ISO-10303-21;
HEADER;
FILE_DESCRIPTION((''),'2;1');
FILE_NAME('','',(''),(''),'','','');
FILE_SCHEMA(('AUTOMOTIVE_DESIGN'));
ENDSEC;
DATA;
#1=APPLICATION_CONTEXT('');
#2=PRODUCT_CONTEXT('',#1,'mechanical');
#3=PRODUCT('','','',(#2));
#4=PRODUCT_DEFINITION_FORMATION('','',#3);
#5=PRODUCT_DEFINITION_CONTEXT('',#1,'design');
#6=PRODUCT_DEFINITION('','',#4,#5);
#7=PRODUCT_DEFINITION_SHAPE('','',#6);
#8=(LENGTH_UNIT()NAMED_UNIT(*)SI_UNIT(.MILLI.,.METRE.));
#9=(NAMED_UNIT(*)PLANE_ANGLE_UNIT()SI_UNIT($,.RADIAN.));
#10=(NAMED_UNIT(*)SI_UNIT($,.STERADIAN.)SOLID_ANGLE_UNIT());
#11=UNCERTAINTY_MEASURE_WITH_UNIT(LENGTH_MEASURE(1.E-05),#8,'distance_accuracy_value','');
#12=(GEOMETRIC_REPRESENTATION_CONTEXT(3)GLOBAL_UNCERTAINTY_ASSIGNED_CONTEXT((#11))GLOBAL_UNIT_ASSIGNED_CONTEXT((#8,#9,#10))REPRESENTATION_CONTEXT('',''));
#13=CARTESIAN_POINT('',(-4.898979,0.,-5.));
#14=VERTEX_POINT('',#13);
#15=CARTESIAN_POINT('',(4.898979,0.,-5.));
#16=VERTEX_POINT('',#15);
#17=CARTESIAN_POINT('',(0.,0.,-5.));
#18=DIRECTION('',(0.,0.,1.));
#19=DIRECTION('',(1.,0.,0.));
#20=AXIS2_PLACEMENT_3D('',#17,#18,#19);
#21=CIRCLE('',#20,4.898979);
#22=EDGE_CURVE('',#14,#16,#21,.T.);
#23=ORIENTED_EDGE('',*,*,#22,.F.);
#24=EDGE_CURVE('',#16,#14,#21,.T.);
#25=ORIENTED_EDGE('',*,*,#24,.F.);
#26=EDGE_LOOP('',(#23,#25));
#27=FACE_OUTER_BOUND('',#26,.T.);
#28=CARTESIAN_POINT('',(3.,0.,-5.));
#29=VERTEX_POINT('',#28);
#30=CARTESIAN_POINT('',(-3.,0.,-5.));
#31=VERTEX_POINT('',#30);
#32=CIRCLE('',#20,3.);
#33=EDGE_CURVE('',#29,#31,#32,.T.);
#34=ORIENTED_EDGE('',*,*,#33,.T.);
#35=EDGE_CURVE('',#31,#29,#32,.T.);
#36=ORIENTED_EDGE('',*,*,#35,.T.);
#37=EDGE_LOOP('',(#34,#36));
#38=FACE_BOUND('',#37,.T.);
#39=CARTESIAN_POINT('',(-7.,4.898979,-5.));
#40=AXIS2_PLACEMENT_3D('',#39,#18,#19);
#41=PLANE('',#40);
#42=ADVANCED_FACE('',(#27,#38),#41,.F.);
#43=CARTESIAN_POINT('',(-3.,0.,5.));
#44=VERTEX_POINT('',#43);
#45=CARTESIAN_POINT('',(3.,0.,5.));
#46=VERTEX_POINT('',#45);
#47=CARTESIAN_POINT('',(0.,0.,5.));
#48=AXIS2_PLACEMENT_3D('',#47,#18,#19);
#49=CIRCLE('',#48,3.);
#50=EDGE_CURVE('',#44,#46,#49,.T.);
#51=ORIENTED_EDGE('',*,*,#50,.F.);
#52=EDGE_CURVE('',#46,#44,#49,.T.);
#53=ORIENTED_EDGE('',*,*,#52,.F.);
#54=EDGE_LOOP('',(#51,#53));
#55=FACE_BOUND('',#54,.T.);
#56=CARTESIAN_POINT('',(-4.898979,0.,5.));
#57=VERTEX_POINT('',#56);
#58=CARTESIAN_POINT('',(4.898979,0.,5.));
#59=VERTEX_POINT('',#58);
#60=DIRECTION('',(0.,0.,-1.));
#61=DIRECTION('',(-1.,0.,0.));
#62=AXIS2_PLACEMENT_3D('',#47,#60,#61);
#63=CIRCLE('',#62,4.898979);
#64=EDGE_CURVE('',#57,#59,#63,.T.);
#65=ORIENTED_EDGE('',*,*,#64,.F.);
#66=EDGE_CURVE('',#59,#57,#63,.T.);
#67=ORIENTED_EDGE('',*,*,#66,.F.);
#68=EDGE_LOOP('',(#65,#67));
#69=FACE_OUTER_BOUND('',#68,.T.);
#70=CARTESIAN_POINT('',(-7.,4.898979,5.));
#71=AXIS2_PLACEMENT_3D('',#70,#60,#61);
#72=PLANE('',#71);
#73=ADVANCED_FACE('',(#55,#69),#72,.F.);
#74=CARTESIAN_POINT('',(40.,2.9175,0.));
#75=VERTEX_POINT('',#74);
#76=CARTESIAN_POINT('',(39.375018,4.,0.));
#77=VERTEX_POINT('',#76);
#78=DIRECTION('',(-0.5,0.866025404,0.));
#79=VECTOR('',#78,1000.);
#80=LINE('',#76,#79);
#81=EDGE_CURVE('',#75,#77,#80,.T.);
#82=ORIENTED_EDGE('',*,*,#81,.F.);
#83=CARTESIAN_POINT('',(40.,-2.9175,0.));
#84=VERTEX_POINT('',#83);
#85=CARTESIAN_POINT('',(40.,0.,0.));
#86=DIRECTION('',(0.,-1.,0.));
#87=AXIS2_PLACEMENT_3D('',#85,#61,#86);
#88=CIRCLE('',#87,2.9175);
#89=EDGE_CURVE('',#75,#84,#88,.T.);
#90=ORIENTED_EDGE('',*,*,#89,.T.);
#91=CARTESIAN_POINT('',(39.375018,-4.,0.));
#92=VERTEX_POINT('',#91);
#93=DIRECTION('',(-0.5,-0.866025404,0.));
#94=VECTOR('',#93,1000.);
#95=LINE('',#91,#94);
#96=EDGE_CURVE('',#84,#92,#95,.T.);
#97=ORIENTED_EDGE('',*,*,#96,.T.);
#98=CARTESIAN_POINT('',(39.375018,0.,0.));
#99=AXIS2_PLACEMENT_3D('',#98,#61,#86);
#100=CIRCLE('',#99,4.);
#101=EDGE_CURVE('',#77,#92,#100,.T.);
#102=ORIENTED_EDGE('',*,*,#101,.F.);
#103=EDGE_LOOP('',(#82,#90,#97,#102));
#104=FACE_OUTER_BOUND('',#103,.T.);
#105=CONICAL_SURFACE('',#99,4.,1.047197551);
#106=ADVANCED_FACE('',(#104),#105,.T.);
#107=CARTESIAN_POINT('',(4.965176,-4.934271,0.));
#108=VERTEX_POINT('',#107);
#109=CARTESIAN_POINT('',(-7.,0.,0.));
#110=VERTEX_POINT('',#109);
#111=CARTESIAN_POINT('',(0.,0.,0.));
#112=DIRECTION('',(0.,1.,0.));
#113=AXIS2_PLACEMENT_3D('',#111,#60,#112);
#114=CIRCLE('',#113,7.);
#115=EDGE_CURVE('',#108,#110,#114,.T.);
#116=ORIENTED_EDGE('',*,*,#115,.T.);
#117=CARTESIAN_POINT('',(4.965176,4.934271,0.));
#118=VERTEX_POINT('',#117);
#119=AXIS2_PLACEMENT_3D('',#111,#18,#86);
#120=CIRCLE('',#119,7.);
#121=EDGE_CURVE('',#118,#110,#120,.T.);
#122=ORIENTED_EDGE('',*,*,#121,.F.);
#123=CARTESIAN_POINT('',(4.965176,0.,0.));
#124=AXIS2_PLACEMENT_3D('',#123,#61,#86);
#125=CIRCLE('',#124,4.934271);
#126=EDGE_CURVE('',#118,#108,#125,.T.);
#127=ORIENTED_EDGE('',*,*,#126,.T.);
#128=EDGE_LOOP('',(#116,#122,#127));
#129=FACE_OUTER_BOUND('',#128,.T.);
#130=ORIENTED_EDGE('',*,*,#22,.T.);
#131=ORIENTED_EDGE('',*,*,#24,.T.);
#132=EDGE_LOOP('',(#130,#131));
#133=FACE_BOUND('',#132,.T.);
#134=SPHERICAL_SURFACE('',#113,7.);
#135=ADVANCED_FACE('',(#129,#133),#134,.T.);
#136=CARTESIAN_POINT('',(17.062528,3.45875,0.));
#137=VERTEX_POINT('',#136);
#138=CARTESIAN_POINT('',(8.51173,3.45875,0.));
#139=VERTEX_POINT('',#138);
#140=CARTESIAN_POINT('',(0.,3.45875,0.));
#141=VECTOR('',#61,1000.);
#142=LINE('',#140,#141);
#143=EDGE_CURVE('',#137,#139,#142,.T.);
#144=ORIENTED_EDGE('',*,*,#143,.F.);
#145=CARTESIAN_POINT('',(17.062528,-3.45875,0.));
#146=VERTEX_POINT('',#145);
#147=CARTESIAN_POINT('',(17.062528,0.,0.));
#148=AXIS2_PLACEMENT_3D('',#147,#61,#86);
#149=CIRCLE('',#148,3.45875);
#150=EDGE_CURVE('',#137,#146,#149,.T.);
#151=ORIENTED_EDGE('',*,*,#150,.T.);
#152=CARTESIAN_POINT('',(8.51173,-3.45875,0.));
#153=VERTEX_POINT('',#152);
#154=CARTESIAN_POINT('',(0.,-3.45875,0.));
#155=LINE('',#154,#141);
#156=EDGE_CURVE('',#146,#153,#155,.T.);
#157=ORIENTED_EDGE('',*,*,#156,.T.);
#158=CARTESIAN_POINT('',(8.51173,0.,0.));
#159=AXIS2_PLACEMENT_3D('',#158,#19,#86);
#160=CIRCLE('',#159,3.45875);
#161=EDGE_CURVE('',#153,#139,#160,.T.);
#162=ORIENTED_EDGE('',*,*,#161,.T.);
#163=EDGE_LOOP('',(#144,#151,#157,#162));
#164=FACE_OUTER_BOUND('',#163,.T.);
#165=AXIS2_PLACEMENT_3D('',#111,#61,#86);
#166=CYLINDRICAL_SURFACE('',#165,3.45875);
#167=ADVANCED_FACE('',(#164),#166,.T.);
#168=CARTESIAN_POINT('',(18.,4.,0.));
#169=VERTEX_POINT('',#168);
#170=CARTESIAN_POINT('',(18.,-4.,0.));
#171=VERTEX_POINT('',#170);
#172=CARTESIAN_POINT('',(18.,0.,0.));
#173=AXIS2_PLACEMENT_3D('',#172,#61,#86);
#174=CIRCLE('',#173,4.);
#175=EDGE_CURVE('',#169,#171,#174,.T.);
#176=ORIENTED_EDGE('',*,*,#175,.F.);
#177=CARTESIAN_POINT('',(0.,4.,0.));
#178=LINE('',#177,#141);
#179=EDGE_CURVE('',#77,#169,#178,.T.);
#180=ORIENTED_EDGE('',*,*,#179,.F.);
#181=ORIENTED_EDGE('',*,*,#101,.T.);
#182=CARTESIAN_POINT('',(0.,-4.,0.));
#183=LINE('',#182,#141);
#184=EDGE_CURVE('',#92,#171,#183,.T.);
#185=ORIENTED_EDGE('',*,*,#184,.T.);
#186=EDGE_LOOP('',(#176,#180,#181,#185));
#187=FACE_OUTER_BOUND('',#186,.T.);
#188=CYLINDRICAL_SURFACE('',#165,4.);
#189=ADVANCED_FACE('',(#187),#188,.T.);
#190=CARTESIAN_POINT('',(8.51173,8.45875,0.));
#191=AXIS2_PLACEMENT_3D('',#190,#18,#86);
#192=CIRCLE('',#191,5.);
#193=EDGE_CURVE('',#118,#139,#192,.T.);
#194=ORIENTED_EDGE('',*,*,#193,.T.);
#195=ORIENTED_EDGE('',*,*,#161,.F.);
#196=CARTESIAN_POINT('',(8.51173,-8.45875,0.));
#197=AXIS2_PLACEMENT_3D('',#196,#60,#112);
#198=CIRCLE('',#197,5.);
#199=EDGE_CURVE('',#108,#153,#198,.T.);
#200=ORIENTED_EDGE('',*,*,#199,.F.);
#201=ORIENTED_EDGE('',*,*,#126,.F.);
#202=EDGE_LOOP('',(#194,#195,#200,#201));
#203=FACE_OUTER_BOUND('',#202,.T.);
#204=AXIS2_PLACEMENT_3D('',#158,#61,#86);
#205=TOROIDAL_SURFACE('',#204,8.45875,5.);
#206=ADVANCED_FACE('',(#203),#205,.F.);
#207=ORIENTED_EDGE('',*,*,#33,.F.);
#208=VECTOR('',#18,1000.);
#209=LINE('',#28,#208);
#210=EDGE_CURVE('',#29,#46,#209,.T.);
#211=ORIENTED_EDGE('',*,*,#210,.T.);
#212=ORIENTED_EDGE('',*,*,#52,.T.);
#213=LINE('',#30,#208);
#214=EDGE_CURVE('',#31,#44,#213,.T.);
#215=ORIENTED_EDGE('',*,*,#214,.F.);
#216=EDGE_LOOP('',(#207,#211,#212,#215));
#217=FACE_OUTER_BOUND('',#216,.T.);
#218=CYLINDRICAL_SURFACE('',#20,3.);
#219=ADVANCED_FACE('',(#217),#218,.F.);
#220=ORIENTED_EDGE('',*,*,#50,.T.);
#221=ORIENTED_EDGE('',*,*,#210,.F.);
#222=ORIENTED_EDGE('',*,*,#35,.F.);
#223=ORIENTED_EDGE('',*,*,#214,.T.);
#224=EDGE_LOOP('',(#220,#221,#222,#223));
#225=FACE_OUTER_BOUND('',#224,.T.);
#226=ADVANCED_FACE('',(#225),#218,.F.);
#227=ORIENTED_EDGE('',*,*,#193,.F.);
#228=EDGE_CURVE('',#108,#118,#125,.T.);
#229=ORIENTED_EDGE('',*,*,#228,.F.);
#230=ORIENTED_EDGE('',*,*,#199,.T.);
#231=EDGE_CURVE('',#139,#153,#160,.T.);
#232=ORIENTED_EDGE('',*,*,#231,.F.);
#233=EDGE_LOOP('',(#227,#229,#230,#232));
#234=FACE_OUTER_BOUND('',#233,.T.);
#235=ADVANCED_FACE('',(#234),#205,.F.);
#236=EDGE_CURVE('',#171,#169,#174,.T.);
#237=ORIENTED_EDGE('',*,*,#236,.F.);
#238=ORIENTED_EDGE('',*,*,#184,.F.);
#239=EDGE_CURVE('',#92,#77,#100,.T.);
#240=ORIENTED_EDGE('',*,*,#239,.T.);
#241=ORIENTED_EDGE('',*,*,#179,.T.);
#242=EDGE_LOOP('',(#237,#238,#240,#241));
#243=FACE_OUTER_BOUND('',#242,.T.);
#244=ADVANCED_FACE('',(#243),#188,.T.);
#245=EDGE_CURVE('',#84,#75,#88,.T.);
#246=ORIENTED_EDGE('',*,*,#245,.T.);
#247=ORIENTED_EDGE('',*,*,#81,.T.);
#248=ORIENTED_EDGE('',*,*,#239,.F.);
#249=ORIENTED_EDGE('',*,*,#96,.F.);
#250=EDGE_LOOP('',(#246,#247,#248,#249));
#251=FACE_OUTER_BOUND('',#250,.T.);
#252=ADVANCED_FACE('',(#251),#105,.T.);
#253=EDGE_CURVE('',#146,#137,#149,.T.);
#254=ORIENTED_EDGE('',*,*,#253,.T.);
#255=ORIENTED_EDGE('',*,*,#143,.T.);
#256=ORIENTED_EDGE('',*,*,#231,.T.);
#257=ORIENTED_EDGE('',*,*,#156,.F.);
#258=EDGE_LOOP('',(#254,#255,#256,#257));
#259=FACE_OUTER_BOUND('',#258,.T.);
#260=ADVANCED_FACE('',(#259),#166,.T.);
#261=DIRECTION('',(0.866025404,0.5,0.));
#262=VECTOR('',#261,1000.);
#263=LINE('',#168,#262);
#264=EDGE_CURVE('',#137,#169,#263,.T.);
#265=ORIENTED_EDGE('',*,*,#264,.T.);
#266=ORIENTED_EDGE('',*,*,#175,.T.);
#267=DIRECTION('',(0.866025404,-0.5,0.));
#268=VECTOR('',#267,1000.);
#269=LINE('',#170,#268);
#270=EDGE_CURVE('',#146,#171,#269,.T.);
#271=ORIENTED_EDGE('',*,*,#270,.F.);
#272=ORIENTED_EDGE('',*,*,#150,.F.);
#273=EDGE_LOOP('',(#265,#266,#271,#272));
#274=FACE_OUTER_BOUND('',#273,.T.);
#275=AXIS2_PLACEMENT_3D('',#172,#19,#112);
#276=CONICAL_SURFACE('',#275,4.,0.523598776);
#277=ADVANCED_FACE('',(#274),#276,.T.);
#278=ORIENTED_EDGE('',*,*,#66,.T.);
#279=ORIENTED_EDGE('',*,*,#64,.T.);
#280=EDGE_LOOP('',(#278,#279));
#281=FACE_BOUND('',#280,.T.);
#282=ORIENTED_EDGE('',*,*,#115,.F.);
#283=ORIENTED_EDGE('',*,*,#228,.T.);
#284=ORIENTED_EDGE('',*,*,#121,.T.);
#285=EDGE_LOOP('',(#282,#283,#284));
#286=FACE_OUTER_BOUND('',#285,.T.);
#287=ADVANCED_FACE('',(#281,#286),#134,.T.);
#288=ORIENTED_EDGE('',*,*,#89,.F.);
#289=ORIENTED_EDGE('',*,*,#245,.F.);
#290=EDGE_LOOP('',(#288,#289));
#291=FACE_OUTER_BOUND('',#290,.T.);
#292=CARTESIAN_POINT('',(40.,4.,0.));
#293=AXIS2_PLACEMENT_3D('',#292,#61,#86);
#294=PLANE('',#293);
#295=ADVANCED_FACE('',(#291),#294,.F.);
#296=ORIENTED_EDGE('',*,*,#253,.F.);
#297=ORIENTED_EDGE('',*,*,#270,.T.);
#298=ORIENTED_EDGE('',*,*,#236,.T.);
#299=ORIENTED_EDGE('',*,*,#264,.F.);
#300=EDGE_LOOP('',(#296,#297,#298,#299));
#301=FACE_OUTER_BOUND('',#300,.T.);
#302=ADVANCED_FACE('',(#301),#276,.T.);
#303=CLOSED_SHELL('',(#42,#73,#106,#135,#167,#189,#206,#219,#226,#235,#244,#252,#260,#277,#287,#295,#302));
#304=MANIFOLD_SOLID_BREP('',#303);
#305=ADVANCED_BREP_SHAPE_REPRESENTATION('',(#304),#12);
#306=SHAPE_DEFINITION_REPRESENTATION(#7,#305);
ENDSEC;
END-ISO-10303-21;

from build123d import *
from build123d.topology import SkipClean

# Parameters (mm, degrees)
CUT_EXTRUDE1_DEPTH      = 13.124356
CUT_EXTRUDE1_DEPTH_BACK = 13.124356
SKETCH4_R               = 3
CUT_EXTRUDE2_DEPTH      = 16.556349
CHAMFER1_SIZE           = 0.4
FILLET1_R               = 5


with BuildPart() as part:
    # Sketch1 → Boss-Revolve (revolve)
    with BuildSketch(Plane.XY):
        with BuildLine():
            Line((-7, 0), (7, 0))
            ThreePointArc((7, 0), (0, 7), (-7, 0))
        make_face()
    revolve(axis=Axis((-13.286843, 0, 0), (1, 0, 0)))

    # Sketch2 → Cut-Extrude1 (cut, two sides: drawn at the far end of the back side and taken through both)
    with SkipClean():  # the faces are left unmerged after this step: merging them gives an invalid solid
        with BuildSketch(Plane(origin=(0, 0, 0), x_dir=(0, 0, -1), z_dir=(1, 0, 0)).offset(-CUT_EXTRUDE1_DEPTH_BACK)):
            with BuildLine():
                Line((-5, 4.898979), (-5, -4.898979))
                ThreePointArc((-5, -4.898979), (-7, 0), (-5, 4.898979))
            make_face()
            with BuildLine():
                Line((5, 4.898979), (5, -4.898979))
                ThreePointArc((5, -4.898979), (7, 0), (5, 4.898979))
            make_face()
        extrude(amount=CUT_EXTRUDE1_DEPTH + CUT_EXTRUDE1_DEPTH_BACK, mode=Mode.SUBTRACT)

    # Sketch4 → Cut-Extrude2 (cut, through all)
    with SkipClean():  # the faces are left unmerged after this step: merging them gives an invalid solid
        with BuildSketch(Plane.XY.offset(5)):
            Circle(SKETCH4_R)
        extrude(amount=-CUT_EXTRUDE2_DEPTH, mode=Mode.SUBTRACT)

    # Sketch5 → Boss-Revolve1 (revolve)
    with SkipClean():  # the faces are left unmerged after this step: merging them gives an invalid solid
        with BuildSketch(Plane.XY, mode=Mode.PRIVATE) as boss_revolve1_sk:
            Polygon((3.469445, 3.45875), (3.469445, 0), (40, 0), (40, 4), (18, 4), (17.062528, 3.45875), align=None)
        revolve(boss_revolve1_sk.sketch.rotate(Axis((0, 0, 0), (1, 0, 0)), 180), axis=Axis((0, 0, 0), (1, 0, 0)))

    # Chamfer1
    chamfer1_edges = [part.edges().sort_by_distance(p)[0] for p in [
        (40, 4, 0),
    ]]
    chamfer(chamfer1_edges, length=CHAMFER1_SIZE)

    # Sketch6 → Cut-Revolve1 (revolve, cut)
    with SkipClean():  # the faces are left unmerged after this step: merging them gives an invalid solid
        with BuildSketch(Plane.XY, mode=Mode.PRIVATE) as cut_revolve1_sk:
            Polygon((39.375018, 4), (40.624982, 4), (40, 2.9175), align=None)
        revolve(cut_revolve1_sk.sketch.rotate(Axis((0, 0, 0), (1, 0, 0)), 180), axis=Axis((0, 0, 0), (1, 0, 0)), mode=Mode.SUBTRACT)

    # Fillet1
    fillet1_edges = [part.edges().sort_by_distance(p)[0] for p in [
        (6.085807, 0, -3.45875),
    ]]
    fillet(fillet1_edges, radius=FILLET1_R)


solid = part.part
